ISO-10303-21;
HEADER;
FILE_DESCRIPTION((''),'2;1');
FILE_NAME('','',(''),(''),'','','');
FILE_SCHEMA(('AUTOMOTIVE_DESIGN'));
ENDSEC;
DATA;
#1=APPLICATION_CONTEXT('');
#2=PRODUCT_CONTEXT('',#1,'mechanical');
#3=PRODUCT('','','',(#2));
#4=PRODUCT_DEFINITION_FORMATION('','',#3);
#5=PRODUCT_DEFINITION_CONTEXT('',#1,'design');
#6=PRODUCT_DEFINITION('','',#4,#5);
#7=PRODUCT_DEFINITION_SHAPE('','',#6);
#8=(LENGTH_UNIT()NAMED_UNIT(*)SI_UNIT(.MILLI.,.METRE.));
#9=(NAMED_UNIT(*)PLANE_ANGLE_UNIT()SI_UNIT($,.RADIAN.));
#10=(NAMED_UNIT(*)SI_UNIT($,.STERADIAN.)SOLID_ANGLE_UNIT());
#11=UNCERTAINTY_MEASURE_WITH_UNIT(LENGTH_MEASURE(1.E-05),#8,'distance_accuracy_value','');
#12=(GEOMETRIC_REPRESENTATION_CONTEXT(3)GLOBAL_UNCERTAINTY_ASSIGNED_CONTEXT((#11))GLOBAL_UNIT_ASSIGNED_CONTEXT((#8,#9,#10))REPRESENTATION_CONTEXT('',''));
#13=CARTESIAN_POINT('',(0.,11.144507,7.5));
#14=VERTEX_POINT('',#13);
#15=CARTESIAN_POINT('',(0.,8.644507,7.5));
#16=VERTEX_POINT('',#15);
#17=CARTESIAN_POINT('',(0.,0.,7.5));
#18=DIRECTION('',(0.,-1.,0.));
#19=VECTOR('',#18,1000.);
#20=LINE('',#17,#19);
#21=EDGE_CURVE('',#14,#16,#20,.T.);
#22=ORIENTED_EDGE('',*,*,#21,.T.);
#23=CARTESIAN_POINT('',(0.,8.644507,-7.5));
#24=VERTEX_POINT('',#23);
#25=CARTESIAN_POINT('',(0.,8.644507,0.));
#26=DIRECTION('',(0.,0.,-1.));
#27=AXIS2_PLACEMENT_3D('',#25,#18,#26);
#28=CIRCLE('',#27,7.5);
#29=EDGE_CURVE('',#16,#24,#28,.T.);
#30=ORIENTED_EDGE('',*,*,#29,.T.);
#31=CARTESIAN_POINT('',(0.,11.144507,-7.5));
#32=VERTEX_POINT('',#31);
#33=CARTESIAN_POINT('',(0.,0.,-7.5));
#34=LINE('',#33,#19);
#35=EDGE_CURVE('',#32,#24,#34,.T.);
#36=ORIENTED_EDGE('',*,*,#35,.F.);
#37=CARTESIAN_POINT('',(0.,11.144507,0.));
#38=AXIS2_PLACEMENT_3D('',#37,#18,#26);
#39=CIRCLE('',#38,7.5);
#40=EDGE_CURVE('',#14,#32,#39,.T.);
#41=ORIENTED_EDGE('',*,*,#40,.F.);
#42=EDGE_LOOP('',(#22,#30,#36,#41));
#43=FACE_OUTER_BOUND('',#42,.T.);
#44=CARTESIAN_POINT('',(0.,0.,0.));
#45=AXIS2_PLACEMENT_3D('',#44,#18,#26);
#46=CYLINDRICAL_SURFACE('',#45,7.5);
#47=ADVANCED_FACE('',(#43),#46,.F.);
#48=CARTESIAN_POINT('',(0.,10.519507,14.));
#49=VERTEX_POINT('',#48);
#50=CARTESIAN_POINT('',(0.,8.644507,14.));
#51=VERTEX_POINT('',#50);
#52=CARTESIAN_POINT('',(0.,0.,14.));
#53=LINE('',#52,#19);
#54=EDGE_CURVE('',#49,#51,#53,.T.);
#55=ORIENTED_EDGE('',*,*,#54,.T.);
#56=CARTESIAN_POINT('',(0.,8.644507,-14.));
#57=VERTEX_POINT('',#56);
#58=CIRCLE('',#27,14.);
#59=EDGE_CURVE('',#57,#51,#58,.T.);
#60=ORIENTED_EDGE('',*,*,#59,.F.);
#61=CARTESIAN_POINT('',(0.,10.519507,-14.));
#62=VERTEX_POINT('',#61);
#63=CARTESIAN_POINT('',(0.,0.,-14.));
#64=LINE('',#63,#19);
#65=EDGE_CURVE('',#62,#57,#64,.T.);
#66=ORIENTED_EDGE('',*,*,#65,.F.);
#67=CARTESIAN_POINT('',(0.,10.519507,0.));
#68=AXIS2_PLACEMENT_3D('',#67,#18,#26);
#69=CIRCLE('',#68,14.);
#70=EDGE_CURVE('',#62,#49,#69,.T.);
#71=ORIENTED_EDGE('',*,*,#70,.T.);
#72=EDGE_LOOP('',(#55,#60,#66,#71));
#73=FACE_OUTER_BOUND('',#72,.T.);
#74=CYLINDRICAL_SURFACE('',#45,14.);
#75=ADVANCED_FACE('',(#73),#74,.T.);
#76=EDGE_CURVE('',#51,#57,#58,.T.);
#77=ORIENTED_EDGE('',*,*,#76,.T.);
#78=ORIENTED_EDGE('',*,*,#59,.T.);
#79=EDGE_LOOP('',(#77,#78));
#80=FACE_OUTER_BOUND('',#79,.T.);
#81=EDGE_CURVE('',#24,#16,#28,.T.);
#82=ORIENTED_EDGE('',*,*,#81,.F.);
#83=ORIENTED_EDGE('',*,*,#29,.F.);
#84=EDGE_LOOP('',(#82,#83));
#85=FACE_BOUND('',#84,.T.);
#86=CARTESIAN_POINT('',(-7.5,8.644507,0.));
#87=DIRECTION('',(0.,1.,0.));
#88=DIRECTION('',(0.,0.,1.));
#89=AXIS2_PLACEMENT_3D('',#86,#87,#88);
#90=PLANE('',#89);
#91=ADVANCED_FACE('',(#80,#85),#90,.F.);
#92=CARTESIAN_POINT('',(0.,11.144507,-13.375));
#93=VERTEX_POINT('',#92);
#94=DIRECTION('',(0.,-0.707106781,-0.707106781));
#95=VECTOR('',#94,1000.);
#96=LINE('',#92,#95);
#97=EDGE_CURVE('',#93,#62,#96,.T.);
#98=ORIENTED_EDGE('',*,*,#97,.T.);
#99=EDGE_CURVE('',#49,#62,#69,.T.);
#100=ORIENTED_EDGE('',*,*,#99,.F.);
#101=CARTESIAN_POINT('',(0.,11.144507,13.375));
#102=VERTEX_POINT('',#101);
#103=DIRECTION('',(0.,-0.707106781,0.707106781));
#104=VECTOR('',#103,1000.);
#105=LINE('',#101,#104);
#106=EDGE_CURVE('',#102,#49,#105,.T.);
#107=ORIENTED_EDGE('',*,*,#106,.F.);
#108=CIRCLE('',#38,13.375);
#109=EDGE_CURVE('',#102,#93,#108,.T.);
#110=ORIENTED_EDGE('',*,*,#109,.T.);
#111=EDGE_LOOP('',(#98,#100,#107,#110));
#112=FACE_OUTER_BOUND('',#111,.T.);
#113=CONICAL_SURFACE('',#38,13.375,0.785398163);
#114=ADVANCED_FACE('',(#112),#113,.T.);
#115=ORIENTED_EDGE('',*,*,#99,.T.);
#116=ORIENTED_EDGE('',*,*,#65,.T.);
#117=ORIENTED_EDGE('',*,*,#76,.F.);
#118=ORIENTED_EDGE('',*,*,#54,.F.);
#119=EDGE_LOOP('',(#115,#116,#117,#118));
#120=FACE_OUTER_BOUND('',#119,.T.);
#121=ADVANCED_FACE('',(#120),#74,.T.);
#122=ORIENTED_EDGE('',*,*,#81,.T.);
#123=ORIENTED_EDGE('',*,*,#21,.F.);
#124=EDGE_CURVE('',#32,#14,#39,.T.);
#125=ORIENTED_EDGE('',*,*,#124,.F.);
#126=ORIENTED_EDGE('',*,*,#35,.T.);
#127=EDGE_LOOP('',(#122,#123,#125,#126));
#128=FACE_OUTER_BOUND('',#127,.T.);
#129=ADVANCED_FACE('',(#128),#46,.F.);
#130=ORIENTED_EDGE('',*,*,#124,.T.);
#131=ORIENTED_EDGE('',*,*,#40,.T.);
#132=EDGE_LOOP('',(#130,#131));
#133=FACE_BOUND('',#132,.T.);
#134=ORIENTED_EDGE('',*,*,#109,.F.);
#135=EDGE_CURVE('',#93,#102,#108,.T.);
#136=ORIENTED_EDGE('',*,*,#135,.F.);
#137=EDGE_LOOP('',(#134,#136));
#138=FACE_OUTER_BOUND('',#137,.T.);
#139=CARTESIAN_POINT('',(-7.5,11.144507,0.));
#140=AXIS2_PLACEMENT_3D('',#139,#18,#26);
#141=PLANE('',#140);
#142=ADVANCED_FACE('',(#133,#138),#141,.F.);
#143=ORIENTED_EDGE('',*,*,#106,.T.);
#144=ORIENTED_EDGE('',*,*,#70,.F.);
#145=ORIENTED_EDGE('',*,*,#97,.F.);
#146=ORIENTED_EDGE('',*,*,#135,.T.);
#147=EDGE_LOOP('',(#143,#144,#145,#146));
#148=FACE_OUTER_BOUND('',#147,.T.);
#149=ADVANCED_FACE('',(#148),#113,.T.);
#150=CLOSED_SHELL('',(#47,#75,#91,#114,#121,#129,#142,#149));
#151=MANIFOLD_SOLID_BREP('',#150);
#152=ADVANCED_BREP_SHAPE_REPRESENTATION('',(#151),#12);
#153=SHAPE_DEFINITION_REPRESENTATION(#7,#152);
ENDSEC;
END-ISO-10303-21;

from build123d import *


with BuildPart() as part:
    # Sketch1 → Base-Revolve (revolve)
    with BuildSketch(Plane.XY, mode=Mode.PRIVATE) as base_revolve_sk:
        Polygon((-13.375, 11.144507042), (-14, 10.519507042), (-14, 8.644507042), (-7.5, 8.644507042), (-7.5, 11.144507042), align=None)
    revolve(base_revolve_sk.sketch.rotate(Axis((0, 0, 0), (0, 1, 0)), 270), axis=Axis((0, 0, 0), (0, 1, 0)))


solid = part.part
